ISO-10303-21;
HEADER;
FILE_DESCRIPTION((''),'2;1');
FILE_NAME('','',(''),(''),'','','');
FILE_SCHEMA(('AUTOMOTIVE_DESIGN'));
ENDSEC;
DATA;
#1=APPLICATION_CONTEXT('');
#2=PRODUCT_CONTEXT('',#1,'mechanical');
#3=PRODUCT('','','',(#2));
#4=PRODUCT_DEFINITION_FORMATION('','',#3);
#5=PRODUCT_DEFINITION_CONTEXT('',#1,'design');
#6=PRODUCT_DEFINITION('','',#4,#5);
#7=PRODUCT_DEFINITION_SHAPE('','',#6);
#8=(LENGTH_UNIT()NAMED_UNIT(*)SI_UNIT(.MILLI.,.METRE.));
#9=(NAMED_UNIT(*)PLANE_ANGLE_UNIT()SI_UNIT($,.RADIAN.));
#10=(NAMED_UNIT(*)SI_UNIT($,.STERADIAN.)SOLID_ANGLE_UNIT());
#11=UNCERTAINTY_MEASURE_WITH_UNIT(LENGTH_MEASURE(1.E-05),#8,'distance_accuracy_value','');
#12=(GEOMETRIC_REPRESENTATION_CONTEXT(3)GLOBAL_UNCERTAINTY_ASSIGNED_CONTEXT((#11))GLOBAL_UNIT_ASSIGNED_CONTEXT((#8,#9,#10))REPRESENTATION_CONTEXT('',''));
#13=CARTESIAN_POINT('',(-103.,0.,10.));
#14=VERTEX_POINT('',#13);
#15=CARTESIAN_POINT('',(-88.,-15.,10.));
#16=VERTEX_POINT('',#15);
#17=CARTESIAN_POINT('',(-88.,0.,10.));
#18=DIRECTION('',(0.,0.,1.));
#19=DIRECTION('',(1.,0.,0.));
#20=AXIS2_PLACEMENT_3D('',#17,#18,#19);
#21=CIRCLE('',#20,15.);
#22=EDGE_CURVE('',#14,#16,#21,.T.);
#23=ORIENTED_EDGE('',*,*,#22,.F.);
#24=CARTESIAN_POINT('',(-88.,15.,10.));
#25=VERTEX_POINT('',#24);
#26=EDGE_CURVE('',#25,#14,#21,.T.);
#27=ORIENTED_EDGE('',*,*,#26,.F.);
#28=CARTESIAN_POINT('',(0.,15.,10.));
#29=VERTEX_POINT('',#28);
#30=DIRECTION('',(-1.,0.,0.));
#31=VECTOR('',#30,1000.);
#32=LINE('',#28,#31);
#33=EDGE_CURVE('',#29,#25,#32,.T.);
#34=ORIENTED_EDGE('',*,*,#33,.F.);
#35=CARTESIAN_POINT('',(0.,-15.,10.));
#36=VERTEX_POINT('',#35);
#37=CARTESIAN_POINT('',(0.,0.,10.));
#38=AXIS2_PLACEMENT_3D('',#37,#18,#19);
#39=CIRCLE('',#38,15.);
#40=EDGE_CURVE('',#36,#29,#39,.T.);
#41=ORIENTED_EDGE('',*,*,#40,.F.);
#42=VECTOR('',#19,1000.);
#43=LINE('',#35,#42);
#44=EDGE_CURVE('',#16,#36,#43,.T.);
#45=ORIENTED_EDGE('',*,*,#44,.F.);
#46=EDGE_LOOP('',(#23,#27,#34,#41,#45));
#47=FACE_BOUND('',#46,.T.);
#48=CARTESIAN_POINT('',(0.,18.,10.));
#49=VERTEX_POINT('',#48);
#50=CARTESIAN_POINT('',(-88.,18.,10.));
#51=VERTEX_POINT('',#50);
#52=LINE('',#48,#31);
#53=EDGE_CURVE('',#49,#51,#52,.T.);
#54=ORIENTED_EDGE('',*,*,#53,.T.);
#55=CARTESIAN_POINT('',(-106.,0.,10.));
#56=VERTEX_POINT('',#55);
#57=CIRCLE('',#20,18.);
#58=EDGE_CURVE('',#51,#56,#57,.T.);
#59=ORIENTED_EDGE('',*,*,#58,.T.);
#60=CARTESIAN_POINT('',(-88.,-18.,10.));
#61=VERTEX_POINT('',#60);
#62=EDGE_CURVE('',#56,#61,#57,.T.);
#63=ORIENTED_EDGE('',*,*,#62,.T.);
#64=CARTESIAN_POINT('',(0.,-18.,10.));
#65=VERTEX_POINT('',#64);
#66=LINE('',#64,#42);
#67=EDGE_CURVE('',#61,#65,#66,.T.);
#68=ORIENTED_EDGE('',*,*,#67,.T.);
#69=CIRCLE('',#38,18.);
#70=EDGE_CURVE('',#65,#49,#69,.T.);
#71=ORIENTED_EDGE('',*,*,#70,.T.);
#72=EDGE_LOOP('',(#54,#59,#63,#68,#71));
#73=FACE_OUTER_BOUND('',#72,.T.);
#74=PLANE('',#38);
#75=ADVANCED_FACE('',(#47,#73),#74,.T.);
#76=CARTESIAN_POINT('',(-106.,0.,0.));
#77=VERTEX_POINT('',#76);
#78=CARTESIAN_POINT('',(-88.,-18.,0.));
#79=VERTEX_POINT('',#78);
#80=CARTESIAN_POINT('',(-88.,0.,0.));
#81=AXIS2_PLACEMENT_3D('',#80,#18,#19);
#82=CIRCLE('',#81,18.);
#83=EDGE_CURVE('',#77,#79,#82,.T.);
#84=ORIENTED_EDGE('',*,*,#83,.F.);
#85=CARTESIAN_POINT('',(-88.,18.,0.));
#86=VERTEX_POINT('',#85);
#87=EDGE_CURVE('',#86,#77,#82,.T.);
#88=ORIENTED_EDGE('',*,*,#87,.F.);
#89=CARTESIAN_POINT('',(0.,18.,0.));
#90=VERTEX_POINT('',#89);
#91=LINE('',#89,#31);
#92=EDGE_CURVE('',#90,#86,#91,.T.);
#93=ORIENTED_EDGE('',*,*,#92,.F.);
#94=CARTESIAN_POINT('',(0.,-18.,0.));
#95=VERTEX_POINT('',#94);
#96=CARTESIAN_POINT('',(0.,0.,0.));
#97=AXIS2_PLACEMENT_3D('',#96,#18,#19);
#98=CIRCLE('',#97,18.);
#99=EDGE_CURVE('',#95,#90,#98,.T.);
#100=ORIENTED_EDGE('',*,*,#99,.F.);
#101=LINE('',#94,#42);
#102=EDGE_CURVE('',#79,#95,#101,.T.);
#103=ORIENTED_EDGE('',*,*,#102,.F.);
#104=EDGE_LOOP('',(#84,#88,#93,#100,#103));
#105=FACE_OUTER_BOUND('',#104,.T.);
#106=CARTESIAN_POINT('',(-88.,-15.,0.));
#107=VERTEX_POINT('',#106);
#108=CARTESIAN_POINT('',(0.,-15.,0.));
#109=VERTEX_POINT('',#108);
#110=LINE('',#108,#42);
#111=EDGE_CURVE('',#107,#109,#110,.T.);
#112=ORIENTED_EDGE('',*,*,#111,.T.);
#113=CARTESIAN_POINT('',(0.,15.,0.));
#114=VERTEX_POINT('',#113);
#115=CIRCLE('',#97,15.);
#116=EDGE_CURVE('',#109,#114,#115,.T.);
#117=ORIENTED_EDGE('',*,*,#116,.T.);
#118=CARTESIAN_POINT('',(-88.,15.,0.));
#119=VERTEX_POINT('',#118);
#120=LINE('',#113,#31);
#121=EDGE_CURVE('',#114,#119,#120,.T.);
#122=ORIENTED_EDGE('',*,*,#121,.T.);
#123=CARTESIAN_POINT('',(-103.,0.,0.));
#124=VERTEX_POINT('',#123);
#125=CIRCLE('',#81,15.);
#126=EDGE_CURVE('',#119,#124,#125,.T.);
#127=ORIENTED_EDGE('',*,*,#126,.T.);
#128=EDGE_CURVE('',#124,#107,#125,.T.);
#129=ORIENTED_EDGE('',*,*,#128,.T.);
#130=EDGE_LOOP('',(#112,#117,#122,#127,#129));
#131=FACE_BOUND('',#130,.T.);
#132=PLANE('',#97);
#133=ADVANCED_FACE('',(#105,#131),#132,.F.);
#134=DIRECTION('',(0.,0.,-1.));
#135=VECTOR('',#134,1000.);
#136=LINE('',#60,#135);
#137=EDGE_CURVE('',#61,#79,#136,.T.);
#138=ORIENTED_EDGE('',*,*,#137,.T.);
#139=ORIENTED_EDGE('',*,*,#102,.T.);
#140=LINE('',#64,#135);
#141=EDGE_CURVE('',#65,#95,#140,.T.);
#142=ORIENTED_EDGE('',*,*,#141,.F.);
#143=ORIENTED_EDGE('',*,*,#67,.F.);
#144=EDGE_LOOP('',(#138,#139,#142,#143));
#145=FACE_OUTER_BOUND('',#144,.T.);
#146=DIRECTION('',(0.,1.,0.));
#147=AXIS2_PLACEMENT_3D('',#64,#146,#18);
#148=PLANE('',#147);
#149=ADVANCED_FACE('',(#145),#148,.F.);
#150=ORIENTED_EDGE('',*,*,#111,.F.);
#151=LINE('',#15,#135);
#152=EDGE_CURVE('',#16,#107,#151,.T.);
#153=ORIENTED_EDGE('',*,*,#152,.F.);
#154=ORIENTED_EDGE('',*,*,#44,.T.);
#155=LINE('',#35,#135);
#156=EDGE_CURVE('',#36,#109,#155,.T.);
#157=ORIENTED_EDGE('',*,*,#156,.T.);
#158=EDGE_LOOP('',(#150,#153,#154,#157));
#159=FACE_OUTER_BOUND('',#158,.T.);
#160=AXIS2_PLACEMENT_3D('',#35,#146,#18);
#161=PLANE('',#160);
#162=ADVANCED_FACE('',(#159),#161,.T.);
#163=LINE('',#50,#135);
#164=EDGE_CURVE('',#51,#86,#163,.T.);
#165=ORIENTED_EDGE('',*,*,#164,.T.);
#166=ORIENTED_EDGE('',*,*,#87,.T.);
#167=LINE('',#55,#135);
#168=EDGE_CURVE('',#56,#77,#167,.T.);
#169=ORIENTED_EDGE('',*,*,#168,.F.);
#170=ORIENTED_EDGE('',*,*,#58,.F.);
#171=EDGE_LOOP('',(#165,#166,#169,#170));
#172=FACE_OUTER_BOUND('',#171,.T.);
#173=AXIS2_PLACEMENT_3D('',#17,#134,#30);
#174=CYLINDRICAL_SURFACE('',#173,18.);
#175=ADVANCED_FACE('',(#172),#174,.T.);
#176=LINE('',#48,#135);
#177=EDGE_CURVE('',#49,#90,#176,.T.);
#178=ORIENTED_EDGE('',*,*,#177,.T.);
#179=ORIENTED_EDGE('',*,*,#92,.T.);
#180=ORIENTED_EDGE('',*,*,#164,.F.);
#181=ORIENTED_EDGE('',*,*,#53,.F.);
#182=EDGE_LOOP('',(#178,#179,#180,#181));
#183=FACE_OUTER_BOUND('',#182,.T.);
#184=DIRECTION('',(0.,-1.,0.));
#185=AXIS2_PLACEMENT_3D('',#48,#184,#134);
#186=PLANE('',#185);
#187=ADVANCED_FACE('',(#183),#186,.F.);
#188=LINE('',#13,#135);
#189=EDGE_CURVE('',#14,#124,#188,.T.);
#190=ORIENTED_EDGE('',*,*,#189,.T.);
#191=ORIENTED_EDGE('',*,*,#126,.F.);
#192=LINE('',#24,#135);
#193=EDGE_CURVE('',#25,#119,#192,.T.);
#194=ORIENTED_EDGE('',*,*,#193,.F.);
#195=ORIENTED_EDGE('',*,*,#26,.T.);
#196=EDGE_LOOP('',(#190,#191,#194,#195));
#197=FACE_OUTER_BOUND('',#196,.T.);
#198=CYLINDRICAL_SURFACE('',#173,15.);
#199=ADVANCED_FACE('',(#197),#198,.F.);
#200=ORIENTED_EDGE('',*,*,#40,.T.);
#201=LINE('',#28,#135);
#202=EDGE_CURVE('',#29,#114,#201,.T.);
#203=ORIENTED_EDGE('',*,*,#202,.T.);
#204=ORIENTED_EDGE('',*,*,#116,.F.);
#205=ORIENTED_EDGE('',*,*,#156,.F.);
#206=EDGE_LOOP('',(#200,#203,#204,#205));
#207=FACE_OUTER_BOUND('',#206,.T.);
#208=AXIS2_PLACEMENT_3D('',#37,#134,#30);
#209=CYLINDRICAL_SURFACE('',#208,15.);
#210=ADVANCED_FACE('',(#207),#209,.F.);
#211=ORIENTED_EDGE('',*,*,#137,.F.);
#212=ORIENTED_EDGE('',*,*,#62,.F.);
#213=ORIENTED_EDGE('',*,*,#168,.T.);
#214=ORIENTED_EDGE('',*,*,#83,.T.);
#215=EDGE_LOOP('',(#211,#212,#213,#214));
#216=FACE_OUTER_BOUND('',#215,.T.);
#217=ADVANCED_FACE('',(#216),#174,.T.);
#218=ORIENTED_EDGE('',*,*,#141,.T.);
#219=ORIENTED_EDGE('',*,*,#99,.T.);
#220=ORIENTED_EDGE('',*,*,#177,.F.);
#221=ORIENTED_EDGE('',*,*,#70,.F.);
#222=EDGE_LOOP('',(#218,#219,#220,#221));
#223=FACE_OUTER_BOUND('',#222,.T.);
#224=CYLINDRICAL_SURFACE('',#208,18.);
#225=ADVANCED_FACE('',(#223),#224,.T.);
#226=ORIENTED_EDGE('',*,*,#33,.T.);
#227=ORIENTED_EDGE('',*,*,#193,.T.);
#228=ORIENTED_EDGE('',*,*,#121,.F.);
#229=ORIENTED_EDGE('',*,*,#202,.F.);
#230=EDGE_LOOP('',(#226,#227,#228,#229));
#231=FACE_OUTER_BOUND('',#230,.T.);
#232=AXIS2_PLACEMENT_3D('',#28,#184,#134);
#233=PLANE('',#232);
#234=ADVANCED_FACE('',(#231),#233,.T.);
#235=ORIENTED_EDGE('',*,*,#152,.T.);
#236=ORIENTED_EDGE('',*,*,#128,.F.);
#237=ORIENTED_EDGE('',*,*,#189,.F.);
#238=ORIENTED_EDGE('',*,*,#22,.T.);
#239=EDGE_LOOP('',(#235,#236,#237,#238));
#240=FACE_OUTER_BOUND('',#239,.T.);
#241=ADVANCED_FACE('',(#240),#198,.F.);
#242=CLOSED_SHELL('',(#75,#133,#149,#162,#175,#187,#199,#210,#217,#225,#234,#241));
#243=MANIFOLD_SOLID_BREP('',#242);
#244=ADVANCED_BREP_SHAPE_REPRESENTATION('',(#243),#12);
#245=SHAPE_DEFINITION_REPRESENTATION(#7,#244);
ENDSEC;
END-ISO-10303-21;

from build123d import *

# Parameters (mm, degrees)
BOSS_EXTRUDE1_DEPTH = 10
SHELL1_T            = -3


with BuildPart() as part:
    # Sketch2 → Boss-Extrude1 (new body)
    with BuildSketch(Plane.XY):
        with BuildLine():
            Line((0, 18), (-88, 18))
            ThreePointArc((-88, 18), (-106, 0), (-88, -18))
            Line((-88, -18), (0, -18))
            ThreePointArc((0, -18), (18, 0), (0, 18))
        make_face()
    extrude(amount=BOSS_EXTRUDE1_DEPTH)

    # Shell1
    shell1_openings = [part.faces().sort_by_distance(p)[0] for p in [
        (-44, 0, 10),
        (-44, 0, 0),
    ]]
    offset(amount=SHELL1_T, openings=shell1_openings, kind=Kind.INTERSECTION)


solid = part.part
